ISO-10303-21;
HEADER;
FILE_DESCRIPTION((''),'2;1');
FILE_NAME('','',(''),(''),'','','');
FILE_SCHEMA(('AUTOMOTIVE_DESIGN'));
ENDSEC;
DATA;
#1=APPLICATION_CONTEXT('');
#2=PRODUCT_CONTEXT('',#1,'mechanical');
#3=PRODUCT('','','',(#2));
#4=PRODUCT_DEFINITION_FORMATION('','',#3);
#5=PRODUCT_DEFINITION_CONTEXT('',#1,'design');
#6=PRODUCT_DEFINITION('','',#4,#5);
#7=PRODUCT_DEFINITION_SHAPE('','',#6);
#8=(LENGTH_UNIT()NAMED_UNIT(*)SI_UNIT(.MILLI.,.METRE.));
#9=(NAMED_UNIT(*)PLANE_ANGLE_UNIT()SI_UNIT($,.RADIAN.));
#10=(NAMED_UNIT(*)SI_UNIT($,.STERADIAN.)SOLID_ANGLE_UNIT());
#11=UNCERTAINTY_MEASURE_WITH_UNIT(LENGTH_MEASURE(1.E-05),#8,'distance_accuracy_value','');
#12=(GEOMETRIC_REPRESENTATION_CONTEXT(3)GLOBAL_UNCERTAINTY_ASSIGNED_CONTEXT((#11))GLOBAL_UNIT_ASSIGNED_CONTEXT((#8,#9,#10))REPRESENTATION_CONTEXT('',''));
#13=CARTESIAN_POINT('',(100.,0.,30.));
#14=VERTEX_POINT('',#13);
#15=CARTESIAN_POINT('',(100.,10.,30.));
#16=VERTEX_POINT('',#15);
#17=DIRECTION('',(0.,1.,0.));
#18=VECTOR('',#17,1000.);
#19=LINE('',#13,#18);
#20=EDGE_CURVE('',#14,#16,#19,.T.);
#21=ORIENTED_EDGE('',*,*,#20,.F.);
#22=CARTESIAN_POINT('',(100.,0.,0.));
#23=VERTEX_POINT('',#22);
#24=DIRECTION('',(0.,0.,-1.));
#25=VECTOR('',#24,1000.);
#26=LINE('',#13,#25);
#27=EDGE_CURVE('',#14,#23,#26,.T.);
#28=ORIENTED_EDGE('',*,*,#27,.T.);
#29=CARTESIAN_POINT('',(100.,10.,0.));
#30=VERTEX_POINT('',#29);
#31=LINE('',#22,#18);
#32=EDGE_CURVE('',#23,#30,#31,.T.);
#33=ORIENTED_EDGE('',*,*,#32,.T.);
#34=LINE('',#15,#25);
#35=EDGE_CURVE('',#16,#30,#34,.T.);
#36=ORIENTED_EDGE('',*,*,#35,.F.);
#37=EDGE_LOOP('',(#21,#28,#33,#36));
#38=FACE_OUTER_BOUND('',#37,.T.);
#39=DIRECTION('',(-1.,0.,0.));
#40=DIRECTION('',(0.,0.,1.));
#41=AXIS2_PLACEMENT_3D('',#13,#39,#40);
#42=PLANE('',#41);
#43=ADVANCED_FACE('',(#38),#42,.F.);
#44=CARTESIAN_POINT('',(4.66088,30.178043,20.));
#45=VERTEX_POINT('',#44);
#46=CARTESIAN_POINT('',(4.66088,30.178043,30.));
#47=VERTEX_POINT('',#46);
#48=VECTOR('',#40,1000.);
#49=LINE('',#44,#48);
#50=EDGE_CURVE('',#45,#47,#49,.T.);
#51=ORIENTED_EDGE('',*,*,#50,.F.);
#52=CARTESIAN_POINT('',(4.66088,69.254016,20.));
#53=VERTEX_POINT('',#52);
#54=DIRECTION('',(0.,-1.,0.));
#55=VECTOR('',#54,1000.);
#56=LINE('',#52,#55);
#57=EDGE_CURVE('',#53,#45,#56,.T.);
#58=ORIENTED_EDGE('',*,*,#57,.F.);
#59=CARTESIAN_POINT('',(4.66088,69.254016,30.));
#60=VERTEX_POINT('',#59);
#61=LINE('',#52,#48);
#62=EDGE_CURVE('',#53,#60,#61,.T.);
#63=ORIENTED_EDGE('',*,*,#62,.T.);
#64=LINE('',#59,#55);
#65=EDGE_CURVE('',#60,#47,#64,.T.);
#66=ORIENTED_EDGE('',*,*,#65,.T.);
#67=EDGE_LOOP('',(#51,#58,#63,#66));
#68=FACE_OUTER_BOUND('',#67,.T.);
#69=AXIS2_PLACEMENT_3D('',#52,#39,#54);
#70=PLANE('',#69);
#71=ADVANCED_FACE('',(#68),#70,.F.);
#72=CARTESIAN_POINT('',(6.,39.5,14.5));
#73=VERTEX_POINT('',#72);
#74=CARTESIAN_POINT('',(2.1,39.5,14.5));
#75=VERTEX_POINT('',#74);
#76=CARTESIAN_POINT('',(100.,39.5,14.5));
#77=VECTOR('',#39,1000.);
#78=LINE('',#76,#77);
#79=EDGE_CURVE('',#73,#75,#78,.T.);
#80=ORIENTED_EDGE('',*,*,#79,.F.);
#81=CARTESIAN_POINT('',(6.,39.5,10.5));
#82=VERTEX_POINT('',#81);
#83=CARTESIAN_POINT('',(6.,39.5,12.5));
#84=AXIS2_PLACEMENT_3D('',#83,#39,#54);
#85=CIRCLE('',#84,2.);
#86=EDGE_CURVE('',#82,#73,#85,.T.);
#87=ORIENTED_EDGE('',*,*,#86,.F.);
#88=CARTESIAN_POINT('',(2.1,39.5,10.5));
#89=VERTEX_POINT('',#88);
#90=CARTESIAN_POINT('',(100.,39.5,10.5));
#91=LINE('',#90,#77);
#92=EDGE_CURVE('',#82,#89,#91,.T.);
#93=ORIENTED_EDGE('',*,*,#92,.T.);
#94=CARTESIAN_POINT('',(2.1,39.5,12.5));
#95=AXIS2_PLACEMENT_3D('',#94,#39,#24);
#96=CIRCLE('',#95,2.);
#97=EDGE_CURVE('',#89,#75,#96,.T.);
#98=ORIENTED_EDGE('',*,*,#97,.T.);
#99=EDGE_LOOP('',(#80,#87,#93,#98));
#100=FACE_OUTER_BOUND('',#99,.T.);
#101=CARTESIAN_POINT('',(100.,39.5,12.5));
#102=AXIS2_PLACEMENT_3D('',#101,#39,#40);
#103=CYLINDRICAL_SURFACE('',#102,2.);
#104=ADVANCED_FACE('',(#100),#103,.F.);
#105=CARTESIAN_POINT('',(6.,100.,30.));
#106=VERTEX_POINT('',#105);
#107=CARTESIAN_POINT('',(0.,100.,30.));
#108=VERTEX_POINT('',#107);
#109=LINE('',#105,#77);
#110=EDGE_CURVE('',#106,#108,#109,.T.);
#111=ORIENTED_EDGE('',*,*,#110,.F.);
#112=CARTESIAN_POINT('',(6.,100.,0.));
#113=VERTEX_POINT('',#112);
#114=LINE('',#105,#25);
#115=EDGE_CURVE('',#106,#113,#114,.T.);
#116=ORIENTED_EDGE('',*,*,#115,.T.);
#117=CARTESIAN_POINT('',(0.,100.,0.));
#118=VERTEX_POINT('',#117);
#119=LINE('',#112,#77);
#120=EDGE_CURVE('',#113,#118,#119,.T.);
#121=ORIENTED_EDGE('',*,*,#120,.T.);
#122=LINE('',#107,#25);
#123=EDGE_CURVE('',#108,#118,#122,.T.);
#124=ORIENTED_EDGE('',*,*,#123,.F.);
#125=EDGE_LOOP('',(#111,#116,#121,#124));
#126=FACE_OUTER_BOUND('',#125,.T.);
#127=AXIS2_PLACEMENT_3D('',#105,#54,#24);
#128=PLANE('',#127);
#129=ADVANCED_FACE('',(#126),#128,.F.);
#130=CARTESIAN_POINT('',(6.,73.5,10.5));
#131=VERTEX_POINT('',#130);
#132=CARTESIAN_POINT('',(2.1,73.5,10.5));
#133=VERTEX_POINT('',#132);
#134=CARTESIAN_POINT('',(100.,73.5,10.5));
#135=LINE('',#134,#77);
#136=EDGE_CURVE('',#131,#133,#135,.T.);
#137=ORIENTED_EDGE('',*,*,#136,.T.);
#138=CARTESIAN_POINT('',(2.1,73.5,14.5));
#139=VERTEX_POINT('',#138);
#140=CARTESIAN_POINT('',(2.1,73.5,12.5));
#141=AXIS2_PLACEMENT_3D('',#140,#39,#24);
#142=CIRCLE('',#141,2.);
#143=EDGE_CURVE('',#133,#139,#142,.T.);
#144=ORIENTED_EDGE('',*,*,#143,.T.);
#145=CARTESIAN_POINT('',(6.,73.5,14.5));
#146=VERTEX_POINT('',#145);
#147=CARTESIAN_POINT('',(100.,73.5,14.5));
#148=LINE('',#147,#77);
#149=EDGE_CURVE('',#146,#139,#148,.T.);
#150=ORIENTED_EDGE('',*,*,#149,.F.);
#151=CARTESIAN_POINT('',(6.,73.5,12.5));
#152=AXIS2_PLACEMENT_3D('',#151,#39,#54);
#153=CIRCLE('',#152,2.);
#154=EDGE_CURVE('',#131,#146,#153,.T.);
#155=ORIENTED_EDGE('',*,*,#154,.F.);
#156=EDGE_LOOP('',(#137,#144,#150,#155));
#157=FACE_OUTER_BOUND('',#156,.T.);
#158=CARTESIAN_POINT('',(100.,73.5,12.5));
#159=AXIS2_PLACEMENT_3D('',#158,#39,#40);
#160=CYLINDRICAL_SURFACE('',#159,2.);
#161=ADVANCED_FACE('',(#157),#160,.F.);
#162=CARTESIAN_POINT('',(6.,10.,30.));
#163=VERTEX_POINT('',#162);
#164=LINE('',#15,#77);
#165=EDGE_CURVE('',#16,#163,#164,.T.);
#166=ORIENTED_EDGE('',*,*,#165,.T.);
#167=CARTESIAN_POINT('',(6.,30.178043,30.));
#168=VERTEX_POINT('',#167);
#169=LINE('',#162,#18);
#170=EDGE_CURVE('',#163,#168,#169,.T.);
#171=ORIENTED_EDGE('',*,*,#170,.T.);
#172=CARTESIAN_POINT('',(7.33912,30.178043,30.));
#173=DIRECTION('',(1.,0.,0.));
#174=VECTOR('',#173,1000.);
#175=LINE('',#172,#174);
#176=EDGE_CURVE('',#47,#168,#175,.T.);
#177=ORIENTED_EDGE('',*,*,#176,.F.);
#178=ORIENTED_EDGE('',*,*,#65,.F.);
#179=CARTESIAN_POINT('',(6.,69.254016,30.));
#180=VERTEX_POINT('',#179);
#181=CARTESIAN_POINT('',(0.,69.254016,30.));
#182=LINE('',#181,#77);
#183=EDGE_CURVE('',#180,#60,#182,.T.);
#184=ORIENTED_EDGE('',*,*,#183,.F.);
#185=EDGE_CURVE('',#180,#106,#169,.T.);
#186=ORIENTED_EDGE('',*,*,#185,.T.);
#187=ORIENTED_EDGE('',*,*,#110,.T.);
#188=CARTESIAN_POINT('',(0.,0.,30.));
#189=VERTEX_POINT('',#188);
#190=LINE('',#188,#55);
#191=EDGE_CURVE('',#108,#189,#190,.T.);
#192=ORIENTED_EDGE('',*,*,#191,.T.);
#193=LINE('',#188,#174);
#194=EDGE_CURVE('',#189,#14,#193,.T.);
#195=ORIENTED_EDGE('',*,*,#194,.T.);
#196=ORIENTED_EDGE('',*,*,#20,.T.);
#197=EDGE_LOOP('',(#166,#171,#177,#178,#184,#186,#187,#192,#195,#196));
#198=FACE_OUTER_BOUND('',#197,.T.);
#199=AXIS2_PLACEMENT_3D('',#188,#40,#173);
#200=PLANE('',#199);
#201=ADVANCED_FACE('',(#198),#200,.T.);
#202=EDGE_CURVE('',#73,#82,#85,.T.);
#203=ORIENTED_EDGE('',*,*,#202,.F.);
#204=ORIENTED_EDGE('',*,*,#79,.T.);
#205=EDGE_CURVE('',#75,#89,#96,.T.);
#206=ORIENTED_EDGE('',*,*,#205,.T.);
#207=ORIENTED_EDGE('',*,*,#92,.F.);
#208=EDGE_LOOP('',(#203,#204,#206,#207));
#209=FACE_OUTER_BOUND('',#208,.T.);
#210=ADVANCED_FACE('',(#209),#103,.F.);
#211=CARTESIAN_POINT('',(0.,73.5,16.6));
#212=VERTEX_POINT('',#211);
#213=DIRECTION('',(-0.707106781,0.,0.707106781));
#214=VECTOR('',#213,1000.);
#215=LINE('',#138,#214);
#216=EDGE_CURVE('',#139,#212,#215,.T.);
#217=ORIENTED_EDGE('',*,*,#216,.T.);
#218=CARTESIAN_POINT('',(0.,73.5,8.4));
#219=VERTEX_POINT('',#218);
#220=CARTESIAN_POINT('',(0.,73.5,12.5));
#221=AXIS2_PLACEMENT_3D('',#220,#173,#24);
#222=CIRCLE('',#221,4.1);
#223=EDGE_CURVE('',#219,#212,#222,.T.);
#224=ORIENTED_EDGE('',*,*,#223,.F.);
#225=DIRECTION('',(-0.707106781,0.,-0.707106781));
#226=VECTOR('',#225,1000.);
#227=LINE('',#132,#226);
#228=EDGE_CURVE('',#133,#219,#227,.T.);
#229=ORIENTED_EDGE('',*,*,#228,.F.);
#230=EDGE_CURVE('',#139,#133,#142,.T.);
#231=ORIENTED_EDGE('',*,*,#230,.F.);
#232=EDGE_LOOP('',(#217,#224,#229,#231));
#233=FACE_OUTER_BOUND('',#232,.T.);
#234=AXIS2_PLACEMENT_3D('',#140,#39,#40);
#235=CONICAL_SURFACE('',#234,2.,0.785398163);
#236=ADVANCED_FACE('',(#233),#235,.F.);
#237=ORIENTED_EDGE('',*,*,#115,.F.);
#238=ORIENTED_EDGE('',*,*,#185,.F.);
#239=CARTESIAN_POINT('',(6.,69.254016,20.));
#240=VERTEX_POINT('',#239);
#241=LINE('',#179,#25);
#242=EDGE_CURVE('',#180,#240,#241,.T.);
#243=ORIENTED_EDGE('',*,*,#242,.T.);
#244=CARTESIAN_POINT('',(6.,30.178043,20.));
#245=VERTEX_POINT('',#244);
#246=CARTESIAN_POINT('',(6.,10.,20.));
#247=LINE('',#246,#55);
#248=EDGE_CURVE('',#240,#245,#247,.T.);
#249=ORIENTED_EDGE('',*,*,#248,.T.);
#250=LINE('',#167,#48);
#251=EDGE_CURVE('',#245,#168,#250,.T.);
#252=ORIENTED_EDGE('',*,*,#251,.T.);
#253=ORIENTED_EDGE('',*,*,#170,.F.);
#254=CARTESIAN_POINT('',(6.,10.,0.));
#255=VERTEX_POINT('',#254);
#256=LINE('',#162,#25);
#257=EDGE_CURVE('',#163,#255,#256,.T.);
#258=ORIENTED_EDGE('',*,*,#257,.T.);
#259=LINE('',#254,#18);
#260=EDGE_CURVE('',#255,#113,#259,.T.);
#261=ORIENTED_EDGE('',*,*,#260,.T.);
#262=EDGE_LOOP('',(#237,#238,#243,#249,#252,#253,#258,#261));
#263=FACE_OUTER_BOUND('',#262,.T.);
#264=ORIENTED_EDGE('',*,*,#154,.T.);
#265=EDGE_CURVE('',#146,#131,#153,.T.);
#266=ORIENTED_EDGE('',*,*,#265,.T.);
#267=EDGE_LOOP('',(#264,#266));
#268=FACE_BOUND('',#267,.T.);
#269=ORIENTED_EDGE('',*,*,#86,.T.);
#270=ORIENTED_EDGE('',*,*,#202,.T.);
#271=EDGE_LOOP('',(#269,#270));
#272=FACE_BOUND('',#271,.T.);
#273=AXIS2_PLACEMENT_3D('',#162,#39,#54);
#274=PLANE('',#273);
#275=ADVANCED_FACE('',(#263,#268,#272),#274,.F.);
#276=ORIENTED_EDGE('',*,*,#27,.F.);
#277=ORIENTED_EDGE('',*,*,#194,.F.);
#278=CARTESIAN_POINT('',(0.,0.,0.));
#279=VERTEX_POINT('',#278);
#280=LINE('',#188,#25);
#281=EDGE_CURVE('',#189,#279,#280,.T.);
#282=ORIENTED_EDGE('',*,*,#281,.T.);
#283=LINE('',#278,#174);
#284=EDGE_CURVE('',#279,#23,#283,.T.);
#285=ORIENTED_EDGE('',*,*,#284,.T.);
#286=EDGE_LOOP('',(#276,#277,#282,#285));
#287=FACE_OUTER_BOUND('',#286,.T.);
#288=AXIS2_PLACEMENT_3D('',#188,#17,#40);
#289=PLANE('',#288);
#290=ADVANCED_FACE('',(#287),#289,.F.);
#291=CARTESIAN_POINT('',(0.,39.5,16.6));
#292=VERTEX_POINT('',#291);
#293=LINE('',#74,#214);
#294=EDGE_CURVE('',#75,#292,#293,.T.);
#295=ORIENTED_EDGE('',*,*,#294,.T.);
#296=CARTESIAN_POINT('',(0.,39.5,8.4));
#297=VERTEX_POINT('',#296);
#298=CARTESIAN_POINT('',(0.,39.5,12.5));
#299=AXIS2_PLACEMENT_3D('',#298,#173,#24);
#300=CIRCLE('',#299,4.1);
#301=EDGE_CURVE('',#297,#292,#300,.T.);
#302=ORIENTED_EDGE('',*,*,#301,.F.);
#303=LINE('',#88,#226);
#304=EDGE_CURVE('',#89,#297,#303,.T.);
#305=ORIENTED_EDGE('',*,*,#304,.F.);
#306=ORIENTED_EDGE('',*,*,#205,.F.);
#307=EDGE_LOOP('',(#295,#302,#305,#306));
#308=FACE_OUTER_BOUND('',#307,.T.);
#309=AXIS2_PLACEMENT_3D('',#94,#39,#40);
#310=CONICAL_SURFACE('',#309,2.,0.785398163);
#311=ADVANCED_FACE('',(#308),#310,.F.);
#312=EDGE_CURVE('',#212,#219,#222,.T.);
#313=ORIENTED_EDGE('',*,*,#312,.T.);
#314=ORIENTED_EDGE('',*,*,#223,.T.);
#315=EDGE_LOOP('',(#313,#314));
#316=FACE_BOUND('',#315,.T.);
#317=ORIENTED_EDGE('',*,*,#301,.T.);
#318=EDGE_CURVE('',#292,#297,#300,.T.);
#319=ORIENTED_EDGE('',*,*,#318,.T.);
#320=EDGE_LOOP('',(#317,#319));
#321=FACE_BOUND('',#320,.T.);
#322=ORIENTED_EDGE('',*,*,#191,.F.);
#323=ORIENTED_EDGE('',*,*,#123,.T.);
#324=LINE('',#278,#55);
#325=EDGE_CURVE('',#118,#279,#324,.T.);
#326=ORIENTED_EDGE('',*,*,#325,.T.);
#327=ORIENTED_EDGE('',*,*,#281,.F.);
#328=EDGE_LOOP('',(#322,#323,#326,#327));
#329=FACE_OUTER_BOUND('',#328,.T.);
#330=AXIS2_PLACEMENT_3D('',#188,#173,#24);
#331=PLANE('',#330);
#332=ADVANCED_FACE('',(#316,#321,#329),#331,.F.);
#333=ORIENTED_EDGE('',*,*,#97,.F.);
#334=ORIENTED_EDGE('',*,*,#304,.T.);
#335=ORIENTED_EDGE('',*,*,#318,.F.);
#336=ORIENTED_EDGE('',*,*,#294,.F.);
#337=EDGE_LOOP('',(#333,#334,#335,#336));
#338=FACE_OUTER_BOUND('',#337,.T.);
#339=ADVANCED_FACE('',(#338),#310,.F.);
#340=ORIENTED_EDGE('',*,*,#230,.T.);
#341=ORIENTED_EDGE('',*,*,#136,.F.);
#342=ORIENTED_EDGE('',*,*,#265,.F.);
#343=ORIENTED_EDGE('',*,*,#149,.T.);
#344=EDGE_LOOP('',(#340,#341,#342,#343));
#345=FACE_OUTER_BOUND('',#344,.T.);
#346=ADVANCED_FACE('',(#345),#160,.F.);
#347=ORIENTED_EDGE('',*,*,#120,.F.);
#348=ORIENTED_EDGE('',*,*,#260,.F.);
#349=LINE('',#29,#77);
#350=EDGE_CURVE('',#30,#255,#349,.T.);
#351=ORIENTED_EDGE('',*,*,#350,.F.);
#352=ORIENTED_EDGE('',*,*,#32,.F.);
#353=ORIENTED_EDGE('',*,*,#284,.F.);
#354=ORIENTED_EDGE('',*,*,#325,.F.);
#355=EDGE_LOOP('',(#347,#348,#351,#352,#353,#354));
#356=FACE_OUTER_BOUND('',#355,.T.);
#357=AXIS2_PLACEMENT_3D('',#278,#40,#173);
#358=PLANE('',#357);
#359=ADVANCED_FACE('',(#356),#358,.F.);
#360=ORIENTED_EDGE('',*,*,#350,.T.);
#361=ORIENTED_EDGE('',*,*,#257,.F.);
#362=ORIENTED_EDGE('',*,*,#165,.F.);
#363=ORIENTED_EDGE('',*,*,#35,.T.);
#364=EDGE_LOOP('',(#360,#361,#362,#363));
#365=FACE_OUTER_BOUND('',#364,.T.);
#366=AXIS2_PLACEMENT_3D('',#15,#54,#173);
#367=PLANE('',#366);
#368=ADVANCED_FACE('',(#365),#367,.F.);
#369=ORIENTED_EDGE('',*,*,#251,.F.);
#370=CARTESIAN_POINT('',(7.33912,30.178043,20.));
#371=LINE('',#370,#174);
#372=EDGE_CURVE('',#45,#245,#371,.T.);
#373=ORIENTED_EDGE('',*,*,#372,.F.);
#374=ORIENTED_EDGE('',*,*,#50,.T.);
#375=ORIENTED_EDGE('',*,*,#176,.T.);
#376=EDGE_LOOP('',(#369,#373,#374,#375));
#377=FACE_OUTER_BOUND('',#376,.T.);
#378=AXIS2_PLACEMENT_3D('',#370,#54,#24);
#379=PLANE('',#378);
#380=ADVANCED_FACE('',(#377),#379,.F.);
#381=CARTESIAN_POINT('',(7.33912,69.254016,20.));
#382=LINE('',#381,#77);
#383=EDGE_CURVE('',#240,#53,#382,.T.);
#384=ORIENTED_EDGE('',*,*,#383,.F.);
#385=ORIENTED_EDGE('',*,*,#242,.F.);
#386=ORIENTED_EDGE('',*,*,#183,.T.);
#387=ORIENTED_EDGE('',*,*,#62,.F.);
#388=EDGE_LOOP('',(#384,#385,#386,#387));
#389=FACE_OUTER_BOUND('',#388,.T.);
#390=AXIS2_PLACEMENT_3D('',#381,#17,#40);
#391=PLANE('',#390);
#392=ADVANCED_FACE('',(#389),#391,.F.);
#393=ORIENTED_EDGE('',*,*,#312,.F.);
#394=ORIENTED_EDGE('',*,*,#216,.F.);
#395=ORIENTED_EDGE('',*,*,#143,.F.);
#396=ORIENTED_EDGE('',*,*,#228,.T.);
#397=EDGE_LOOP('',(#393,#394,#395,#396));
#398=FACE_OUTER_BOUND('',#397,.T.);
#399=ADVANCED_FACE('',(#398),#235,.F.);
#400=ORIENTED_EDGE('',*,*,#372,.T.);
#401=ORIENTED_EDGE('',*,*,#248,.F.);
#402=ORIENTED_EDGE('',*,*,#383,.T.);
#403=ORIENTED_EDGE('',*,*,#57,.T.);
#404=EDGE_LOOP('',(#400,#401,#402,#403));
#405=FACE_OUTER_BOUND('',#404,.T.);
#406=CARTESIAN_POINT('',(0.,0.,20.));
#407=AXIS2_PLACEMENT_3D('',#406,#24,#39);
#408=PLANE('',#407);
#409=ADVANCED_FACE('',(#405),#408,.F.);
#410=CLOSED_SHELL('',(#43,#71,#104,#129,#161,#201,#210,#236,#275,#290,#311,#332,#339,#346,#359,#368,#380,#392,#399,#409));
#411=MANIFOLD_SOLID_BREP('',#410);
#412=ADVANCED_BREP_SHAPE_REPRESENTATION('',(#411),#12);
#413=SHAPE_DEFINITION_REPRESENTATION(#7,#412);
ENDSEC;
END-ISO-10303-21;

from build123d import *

# Parameters (mm, degrees)
BOSS_EXTRUDE1_DEPTH = 30
SKETCH2_R           = 2
CUT_EXTRUDE1_DEPTH  = 145.568322948
CHAMFER1_SIZE       = 2.1
SKETCH3_W           = 2.678240958
SKETCH3_H           = 39.075972863
CUT_EXTRUDE2_DEPTH  = 10


with BuildPart() as part:
    # Sketch1 → Boss-Extrude1 (new body)
    with BuildSketch(Plane.XY):
        Polygon((0, 0), (100, 0), (100, 10), (6, 10), (6, 100), (0, 100), align=None)
    extrude(amount=BOSS_EXTRUDE1_DEPTH)

    # Sketch2 → Cut-Extrude1 (cut, through all)
    with BuildSketch(Plane.ZY):
        with Locations((12.5, 73.5)):
            Circle(SKETCH2_R)
        with Locations((12.5, 39.5)):
            Circle(SKETCH2_R)
    extrude(amount=-CUT_EXTRUDE1_DEPTH, mode=Mode.SUBTRACT)

    # Chamfer1
    chamfer1_edges = [part.edges().sort_by_distance(p)[0] for p in [
        (0, 73.5, 10.5),
        (0, 39.5, 10.5),
    ]]
    chamfer(chamfer1_edges, length=CHAMFER1_SIZE)

    # Sketch3 → Cut-Extrude2 (cut)
    with BuildSketch(Plane.XY.offset(30)):
        with Locations((6, 49.716029753)):
            Rectangle(SKETCH3_W, SKETCH3_H)
    extrude(amount=-CUT_EXTRUDE2_DEPTH, mode=Mode.SUBTRACT)


solid = part.part
